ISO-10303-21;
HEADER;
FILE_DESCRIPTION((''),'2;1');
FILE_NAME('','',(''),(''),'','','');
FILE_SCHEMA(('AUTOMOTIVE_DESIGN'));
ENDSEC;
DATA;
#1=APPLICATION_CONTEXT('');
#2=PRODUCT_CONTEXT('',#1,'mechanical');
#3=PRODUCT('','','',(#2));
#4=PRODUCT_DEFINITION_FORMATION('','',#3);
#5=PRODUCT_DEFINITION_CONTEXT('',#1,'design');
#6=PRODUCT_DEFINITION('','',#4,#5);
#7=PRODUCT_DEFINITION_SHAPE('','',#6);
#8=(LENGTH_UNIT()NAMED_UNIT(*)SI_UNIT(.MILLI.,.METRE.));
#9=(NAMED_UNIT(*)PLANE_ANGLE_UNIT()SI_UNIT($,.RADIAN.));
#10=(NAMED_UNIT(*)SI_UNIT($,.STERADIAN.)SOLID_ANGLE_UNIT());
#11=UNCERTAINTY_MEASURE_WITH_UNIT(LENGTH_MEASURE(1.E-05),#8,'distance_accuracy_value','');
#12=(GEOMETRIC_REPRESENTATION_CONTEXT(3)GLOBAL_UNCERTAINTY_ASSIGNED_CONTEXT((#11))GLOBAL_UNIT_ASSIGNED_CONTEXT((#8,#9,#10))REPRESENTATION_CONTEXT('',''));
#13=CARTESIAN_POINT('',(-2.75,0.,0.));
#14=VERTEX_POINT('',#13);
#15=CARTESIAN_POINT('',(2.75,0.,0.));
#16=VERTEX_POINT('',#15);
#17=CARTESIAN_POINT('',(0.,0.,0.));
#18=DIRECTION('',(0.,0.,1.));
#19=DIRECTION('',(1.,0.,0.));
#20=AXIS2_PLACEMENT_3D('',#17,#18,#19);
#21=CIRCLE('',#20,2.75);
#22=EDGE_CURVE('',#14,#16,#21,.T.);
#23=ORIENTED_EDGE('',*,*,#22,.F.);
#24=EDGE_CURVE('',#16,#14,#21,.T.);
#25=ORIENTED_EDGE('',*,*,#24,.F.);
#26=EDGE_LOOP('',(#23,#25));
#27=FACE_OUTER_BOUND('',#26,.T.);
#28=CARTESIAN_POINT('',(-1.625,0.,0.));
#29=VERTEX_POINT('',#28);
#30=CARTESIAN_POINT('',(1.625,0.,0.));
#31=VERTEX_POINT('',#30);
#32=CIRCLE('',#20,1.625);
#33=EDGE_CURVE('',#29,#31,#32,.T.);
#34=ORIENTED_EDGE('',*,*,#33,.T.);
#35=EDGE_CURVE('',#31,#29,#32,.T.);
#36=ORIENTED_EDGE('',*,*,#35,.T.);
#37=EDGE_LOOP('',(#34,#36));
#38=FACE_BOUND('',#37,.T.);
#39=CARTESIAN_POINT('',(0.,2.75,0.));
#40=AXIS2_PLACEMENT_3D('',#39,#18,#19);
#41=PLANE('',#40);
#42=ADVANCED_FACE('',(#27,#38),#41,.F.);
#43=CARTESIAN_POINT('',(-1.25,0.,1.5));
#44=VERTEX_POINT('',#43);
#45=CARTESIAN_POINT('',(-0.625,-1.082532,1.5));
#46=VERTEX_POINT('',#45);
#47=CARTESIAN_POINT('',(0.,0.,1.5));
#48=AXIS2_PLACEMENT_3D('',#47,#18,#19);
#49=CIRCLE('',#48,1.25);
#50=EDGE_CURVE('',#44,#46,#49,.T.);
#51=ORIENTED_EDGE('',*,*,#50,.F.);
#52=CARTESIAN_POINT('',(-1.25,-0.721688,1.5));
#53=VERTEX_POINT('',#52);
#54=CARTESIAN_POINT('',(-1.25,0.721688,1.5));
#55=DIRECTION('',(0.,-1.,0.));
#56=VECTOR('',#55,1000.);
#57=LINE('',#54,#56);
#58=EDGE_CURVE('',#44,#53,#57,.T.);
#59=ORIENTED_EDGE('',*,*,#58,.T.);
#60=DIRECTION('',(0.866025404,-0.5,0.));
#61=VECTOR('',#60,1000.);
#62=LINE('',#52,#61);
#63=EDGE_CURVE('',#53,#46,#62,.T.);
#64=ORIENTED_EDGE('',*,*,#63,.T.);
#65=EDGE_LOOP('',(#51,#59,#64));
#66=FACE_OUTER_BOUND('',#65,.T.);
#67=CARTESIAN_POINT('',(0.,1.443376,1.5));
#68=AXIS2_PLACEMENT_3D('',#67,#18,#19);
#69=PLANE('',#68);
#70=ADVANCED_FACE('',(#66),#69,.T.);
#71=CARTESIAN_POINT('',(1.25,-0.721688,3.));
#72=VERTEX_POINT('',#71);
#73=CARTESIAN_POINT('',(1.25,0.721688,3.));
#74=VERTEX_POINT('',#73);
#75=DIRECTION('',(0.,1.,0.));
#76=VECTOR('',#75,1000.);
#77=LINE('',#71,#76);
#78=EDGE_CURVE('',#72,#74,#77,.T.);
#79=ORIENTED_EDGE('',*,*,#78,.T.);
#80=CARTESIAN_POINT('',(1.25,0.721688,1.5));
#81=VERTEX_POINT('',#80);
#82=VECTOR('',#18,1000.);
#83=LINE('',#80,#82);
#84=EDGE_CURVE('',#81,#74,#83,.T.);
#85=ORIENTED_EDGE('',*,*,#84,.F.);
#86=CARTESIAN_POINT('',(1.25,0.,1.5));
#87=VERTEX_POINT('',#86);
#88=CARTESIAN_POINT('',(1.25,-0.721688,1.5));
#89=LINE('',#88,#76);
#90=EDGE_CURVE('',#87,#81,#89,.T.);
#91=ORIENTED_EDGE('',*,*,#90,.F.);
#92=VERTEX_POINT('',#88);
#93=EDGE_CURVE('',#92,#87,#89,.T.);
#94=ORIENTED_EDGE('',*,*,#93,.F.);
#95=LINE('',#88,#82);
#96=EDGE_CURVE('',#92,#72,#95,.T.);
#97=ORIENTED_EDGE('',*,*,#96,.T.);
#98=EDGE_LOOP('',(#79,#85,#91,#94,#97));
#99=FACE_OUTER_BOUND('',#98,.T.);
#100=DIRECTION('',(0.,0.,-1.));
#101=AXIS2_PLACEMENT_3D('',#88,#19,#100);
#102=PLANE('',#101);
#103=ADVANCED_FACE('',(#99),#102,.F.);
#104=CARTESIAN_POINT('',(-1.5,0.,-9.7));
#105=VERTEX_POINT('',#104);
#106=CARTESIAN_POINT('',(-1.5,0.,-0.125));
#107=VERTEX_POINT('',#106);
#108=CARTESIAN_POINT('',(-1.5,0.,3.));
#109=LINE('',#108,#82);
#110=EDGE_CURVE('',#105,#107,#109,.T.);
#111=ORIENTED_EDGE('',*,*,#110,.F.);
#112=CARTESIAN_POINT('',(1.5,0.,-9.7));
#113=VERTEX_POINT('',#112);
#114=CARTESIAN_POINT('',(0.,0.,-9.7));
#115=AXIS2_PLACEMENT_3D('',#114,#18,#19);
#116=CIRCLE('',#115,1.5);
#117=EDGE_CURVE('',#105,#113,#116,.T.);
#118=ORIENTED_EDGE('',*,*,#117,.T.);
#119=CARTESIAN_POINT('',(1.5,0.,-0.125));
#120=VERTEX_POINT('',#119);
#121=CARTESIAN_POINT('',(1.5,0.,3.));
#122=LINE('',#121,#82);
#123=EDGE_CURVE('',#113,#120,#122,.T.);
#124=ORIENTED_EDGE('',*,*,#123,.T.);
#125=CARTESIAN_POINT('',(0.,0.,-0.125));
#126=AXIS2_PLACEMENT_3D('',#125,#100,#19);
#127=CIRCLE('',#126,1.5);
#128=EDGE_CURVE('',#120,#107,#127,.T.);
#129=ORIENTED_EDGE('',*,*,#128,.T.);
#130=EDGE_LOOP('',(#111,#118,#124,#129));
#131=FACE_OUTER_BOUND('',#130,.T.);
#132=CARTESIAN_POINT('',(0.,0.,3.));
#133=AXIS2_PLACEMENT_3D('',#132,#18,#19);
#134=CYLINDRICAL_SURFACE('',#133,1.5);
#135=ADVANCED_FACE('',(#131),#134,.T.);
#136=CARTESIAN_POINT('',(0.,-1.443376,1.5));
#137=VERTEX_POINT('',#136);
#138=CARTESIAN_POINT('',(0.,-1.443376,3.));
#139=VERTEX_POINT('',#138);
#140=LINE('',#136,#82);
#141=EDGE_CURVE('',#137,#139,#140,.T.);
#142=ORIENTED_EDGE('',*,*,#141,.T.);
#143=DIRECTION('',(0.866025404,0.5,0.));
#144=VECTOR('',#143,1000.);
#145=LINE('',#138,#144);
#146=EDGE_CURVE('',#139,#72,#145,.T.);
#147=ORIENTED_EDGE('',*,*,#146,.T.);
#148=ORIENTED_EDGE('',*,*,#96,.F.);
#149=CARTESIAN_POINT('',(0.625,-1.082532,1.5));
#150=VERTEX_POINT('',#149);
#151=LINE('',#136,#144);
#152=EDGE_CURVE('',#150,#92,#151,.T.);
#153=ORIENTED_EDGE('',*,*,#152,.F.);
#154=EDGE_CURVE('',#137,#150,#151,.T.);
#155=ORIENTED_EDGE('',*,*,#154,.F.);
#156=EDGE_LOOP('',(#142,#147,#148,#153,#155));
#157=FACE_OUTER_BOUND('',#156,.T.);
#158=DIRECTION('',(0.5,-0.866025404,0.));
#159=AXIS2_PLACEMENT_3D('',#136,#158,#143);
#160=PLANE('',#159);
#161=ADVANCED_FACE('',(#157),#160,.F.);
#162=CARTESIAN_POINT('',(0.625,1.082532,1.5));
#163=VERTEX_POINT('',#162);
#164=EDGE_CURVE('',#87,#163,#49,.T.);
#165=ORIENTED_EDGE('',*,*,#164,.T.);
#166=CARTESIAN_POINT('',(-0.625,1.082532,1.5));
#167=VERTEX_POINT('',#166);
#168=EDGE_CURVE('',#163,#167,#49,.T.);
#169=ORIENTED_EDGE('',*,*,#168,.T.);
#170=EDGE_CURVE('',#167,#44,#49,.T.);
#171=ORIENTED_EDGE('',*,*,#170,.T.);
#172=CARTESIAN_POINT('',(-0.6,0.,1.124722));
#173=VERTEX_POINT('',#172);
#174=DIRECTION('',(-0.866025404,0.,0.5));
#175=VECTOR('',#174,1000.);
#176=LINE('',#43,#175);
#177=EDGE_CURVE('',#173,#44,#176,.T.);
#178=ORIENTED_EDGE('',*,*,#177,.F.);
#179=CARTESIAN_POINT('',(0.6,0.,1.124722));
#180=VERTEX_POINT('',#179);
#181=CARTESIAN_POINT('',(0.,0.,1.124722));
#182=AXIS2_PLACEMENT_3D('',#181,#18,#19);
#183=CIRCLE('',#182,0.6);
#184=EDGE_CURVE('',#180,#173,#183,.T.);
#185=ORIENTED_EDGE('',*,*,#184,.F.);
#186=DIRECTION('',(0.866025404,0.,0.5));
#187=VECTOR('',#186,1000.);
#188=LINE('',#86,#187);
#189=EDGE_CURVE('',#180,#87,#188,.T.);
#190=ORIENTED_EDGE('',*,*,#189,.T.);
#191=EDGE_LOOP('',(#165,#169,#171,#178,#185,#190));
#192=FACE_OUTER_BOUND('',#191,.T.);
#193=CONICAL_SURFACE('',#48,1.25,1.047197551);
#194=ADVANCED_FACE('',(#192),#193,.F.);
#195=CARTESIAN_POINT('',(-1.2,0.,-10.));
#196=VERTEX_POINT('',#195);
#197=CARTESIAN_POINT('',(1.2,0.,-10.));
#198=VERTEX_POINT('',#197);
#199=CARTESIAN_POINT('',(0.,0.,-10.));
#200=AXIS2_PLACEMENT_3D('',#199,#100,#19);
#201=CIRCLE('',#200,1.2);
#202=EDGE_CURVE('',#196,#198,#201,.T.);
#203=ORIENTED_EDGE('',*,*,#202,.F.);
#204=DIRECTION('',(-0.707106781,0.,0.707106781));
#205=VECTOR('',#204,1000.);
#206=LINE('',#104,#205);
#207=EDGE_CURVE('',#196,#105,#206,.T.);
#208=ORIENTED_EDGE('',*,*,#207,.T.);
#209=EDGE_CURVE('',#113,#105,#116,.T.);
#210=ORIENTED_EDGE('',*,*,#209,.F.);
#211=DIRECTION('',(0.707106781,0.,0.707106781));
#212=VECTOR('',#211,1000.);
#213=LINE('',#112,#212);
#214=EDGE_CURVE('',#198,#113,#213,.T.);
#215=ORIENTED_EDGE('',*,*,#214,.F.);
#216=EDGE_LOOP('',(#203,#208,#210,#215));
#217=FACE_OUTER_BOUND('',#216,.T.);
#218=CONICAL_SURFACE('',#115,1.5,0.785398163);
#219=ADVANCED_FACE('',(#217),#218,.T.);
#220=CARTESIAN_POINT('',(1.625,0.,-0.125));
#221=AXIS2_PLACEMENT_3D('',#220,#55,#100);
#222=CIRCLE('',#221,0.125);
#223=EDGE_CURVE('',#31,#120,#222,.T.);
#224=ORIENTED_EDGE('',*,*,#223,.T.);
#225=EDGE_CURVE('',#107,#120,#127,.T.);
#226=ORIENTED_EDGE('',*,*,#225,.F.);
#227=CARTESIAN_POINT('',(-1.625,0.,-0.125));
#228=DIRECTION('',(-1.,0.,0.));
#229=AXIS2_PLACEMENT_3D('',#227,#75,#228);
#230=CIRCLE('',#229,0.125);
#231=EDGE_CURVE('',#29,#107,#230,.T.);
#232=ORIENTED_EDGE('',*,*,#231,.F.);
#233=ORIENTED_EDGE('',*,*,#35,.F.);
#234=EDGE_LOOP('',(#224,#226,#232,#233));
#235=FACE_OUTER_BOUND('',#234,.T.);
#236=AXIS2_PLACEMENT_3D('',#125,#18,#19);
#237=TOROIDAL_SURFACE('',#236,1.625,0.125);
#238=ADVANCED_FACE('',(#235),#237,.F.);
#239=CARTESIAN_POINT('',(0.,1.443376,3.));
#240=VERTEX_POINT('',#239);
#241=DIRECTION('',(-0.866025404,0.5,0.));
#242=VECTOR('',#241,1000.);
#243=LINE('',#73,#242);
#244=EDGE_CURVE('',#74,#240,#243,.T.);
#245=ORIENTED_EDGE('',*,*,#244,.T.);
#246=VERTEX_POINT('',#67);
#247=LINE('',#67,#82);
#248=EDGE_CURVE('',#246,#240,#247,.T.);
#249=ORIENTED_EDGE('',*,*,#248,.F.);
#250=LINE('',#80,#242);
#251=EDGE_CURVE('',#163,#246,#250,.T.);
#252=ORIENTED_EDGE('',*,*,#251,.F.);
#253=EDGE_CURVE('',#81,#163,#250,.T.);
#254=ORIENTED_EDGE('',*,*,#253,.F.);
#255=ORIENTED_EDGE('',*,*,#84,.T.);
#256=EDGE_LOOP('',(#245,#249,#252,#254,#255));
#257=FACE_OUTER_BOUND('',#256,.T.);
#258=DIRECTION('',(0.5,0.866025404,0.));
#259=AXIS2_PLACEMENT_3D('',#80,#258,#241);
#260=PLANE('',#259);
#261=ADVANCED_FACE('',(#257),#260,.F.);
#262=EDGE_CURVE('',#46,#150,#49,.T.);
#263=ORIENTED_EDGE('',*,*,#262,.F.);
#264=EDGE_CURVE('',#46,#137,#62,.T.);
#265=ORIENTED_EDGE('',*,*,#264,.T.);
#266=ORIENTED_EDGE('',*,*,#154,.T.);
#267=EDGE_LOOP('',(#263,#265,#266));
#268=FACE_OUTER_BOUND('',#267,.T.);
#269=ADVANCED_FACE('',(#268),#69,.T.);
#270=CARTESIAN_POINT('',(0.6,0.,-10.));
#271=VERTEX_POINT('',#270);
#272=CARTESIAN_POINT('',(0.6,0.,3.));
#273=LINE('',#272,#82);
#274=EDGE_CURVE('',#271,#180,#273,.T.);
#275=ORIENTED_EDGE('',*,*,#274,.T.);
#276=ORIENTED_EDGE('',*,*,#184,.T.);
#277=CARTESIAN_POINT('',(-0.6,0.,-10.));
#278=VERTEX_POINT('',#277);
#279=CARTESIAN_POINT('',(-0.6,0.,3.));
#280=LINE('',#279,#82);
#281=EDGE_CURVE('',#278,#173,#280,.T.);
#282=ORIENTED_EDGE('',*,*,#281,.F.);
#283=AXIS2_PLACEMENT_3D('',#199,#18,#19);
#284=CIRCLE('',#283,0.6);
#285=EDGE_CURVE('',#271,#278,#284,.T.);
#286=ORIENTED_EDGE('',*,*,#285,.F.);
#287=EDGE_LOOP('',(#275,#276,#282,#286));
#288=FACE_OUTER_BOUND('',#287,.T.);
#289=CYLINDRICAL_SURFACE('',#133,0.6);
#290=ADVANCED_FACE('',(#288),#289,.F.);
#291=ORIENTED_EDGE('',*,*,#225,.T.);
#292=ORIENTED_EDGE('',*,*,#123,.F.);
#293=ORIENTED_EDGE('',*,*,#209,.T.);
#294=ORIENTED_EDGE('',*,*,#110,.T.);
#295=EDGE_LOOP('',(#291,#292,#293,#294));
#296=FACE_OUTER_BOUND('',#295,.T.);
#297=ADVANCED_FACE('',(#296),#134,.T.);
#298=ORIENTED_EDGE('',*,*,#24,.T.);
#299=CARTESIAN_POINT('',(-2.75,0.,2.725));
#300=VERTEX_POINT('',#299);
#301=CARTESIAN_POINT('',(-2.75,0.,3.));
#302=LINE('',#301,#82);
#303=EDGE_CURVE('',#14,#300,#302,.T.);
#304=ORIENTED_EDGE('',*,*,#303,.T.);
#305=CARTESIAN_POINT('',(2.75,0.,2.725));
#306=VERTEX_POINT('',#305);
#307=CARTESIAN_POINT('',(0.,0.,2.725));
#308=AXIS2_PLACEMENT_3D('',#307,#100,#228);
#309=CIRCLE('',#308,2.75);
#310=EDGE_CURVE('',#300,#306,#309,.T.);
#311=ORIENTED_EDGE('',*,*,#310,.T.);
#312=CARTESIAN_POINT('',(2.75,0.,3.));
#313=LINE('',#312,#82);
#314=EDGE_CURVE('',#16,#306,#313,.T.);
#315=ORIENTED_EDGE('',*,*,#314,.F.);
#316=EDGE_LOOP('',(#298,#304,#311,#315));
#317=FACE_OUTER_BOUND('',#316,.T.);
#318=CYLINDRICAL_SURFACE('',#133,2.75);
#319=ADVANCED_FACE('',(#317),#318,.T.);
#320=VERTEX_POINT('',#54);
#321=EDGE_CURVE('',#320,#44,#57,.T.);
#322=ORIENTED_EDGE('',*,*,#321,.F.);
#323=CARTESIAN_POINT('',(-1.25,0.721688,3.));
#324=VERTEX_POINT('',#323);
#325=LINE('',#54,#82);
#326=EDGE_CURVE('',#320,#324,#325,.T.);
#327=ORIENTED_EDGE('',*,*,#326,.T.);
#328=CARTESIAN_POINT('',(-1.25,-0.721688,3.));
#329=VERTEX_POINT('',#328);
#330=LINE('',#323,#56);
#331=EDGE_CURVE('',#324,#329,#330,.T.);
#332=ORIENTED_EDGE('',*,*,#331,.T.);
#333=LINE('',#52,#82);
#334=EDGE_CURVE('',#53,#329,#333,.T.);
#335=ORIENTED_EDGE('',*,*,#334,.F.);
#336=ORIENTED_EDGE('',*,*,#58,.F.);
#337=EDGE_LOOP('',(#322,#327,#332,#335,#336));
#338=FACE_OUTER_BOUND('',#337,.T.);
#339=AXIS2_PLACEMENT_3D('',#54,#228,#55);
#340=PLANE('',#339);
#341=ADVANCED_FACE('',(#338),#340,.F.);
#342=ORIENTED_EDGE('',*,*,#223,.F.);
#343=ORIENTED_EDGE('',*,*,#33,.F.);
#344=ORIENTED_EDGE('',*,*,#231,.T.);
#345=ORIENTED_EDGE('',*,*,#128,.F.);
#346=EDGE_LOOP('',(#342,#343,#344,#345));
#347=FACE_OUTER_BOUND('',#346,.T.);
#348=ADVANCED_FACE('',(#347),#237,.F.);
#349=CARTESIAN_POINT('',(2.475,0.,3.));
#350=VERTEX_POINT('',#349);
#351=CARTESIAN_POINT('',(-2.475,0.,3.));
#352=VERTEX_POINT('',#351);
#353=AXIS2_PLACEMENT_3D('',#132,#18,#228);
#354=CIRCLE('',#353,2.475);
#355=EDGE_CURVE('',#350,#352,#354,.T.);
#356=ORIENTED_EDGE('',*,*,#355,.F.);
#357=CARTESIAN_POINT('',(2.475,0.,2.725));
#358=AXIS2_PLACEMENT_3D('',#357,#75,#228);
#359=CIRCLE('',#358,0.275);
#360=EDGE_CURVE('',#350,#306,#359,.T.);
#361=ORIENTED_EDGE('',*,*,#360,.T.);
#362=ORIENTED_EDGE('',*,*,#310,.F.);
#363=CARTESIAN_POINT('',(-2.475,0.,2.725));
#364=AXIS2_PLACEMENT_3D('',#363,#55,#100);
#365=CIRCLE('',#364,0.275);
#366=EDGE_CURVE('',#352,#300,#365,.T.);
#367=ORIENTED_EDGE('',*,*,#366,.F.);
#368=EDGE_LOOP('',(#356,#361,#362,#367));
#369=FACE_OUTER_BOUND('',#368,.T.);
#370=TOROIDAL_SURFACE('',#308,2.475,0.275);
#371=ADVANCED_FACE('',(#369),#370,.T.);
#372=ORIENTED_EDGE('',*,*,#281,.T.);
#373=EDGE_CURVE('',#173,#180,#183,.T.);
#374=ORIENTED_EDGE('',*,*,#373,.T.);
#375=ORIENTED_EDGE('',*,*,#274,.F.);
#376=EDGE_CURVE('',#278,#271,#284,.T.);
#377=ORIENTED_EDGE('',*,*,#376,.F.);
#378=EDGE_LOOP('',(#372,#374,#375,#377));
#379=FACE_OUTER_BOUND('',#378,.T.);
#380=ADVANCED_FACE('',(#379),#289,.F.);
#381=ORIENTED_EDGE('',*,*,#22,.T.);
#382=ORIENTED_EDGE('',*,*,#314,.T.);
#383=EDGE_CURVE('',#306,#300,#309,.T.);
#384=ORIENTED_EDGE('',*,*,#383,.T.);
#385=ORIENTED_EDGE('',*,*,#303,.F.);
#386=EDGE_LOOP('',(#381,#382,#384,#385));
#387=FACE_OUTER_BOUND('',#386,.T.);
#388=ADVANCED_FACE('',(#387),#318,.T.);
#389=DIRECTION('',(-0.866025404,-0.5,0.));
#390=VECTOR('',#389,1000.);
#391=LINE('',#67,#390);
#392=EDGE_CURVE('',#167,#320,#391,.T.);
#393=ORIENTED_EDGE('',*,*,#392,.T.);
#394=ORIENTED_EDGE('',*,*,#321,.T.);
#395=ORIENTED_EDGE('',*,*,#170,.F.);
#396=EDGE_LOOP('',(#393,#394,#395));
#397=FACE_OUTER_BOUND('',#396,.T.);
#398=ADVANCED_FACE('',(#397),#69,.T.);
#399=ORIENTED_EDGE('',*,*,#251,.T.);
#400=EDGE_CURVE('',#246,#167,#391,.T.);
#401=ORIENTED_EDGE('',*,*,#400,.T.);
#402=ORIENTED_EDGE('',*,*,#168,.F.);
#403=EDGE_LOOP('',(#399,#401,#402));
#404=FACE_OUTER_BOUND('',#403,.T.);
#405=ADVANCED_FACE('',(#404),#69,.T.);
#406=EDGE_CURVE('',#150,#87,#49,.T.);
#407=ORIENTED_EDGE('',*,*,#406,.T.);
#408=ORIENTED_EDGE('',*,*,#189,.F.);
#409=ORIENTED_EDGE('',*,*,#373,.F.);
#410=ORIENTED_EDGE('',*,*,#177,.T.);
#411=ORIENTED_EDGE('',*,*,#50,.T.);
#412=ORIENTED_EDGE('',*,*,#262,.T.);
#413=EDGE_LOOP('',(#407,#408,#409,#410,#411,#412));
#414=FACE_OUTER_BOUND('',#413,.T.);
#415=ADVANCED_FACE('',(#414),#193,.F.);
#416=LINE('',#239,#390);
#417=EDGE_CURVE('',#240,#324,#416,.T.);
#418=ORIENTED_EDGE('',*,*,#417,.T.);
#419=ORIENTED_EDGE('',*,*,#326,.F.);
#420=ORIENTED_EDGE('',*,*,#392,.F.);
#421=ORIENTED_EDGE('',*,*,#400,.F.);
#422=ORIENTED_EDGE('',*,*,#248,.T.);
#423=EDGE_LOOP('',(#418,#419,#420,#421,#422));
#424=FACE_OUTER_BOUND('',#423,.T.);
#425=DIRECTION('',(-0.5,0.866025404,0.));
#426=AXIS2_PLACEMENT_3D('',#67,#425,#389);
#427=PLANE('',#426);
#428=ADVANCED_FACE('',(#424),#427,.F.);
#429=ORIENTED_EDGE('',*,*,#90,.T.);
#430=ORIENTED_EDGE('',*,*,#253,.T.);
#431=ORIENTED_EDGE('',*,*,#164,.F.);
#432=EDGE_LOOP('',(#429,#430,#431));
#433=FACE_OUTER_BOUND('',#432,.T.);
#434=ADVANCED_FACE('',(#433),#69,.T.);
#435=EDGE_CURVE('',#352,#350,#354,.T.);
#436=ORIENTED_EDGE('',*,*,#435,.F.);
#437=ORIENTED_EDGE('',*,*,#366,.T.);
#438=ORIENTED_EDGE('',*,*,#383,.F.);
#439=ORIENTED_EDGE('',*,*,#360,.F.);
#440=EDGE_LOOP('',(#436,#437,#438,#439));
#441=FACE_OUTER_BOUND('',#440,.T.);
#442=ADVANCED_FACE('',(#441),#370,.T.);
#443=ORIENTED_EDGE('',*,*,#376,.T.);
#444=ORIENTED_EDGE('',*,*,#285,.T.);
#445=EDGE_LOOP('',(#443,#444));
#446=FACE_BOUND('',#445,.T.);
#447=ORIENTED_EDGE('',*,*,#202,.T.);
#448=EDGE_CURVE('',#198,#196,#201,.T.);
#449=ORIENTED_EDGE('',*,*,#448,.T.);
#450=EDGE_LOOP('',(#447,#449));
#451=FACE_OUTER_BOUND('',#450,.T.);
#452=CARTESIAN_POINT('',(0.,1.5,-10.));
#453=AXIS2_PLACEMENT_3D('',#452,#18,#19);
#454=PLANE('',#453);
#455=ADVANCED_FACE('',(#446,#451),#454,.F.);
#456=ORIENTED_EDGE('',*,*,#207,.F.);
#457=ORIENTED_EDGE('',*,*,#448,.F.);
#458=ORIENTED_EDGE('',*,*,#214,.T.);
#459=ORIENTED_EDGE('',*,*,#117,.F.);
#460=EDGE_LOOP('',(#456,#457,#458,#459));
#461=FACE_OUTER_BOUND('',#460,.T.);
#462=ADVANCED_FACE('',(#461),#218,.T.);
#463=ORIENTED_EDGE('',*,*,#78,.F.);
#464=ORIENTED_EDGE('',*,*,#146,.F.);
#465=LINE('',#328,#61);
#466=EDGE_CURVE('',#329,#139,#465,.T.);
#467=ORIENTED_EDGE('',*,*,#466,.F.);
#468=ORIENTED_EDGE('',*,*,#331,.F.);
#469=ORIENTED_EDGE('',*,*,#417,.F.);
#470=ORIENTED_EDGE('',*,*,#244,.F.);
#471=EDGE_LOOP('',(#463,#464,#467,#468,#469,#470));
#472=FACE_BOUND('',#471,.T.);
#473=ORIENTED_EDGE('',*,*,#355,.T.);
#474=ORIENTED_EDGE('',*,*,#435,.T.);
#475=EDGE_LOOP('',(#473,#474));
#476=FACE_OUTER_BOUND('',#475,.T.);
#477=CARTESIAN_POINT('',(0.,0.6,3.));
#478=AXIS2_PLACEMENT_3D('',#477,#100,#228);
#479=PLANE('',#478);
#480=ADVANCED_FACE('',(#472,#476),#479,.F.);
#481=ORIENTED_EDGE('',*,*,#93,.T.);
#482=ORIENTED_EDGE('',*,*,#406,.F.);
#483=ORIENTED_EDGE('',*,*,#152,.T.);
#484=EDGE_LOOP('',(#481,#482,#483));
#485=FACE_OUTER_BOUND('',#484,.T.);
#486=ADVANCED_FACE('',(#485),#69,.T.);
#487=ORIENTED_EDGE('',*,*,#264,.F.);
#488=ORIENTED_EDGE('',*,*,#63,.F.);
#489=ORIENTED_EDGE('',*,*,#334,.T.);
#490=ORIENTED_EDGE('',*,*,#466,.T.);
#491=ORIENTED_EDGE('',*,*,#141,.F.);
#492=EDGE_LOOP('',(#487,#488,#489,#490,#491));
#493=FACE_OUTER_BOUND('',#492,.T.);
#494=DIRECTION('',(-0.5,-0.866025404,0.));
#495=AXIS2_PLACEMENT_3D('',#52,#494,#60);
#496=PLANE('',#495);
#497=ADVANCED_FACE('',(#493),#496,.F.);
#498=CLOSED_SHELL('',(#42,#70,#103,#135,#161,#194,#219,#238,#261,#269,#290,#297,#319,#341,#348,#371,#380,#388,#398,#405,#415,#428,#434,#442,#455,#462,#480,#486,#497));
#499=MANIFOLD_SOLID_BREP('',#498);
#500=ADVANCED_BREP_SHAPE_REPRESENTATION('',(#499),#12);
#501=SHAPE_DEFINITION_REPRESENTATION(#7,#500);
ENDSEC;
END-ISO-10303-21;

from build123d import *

# Parameters (mm, degrees)
CUT_EXTRUDE1_DEPTH = 1.5
FILLET1_R          = 0.275
CHAMFER1_SIZE      = 0.3
FILLET2_R          = 0.125


with BuildPart() as part:
    # Sketch3 → Revolve1 (revolve)
    with BuildSketch(Plane(origin=(0, 0, 0), x_dir=(0, 0, -1), z_dir=(1, 0, 0)), mode=Mode.PRIVATE) as revolve1_sk:
        Polygon((-3, 0.6), (-3, 2.75), (0, 2.75), (0, 1.5), (10, 1.5), (10, 0.6), align=None)
    revolve(revolve1_sk.sketch.rotate(Axis((0, 0, 3), (0, 0, -1)), 90), axis=Axis((0, 0, 3), (0, 0, -1)))

    # Sketch4 → Cut-Extrude1 (cut)
    with BuildSketch(Plane.XY.offset(3)):
        Polygon((0, 1.443375673), (-1.25, 0.721687836), (-1.25, -0.721687836), (0, -1.443375673), (1.25, -0.721687836), (1.25, 0.721687836), align=None)
    extrude(amount=-CUT_EXTRUDE1_DEPTH, mode=Mode.SUBTRACT)

    # Fillet1
    fillet1_edges = [part.edges().sort_by_distance(p)[0] for p in [
        (-2.75, 0, 3),
    ]]
    fillet(fillet1_edges, radius=FILLET1_R)

    # Chamfer1
    chamfer1_edges = [part.edges().sort_by_distance(p)[0] for p in [
        (-1.5, 0, -10),
    ]]
    chamfer(chamfer1_edges, length=CHAMFER1_SIZE)

    # Cut-Extrude2 cone 1 section (through the dimple's axis) → Cut-Extrude2 (revolve, cut)
    with BuildSketch(Plane(origin=(0, 0, 1.5), x_dir=(0, -1, 0), z_dir=(1, 0, 0))):
        Polygon((0, 0), (1.25, 0), (0, 0.721687836), align=None)
    revolve(axis=Axis((0, 0, 1.5), (0, 0, -1)), mode=Mode.SUBTRACT)

    # Fillet2
    fillet2_edges = [part.edges().sort_by_distance(p)[0] for p in [
        (-1.5, 0, 0),
    ]]
    fillet(fillet2_edges, radius=FILLET2_R)


solid = part.part
